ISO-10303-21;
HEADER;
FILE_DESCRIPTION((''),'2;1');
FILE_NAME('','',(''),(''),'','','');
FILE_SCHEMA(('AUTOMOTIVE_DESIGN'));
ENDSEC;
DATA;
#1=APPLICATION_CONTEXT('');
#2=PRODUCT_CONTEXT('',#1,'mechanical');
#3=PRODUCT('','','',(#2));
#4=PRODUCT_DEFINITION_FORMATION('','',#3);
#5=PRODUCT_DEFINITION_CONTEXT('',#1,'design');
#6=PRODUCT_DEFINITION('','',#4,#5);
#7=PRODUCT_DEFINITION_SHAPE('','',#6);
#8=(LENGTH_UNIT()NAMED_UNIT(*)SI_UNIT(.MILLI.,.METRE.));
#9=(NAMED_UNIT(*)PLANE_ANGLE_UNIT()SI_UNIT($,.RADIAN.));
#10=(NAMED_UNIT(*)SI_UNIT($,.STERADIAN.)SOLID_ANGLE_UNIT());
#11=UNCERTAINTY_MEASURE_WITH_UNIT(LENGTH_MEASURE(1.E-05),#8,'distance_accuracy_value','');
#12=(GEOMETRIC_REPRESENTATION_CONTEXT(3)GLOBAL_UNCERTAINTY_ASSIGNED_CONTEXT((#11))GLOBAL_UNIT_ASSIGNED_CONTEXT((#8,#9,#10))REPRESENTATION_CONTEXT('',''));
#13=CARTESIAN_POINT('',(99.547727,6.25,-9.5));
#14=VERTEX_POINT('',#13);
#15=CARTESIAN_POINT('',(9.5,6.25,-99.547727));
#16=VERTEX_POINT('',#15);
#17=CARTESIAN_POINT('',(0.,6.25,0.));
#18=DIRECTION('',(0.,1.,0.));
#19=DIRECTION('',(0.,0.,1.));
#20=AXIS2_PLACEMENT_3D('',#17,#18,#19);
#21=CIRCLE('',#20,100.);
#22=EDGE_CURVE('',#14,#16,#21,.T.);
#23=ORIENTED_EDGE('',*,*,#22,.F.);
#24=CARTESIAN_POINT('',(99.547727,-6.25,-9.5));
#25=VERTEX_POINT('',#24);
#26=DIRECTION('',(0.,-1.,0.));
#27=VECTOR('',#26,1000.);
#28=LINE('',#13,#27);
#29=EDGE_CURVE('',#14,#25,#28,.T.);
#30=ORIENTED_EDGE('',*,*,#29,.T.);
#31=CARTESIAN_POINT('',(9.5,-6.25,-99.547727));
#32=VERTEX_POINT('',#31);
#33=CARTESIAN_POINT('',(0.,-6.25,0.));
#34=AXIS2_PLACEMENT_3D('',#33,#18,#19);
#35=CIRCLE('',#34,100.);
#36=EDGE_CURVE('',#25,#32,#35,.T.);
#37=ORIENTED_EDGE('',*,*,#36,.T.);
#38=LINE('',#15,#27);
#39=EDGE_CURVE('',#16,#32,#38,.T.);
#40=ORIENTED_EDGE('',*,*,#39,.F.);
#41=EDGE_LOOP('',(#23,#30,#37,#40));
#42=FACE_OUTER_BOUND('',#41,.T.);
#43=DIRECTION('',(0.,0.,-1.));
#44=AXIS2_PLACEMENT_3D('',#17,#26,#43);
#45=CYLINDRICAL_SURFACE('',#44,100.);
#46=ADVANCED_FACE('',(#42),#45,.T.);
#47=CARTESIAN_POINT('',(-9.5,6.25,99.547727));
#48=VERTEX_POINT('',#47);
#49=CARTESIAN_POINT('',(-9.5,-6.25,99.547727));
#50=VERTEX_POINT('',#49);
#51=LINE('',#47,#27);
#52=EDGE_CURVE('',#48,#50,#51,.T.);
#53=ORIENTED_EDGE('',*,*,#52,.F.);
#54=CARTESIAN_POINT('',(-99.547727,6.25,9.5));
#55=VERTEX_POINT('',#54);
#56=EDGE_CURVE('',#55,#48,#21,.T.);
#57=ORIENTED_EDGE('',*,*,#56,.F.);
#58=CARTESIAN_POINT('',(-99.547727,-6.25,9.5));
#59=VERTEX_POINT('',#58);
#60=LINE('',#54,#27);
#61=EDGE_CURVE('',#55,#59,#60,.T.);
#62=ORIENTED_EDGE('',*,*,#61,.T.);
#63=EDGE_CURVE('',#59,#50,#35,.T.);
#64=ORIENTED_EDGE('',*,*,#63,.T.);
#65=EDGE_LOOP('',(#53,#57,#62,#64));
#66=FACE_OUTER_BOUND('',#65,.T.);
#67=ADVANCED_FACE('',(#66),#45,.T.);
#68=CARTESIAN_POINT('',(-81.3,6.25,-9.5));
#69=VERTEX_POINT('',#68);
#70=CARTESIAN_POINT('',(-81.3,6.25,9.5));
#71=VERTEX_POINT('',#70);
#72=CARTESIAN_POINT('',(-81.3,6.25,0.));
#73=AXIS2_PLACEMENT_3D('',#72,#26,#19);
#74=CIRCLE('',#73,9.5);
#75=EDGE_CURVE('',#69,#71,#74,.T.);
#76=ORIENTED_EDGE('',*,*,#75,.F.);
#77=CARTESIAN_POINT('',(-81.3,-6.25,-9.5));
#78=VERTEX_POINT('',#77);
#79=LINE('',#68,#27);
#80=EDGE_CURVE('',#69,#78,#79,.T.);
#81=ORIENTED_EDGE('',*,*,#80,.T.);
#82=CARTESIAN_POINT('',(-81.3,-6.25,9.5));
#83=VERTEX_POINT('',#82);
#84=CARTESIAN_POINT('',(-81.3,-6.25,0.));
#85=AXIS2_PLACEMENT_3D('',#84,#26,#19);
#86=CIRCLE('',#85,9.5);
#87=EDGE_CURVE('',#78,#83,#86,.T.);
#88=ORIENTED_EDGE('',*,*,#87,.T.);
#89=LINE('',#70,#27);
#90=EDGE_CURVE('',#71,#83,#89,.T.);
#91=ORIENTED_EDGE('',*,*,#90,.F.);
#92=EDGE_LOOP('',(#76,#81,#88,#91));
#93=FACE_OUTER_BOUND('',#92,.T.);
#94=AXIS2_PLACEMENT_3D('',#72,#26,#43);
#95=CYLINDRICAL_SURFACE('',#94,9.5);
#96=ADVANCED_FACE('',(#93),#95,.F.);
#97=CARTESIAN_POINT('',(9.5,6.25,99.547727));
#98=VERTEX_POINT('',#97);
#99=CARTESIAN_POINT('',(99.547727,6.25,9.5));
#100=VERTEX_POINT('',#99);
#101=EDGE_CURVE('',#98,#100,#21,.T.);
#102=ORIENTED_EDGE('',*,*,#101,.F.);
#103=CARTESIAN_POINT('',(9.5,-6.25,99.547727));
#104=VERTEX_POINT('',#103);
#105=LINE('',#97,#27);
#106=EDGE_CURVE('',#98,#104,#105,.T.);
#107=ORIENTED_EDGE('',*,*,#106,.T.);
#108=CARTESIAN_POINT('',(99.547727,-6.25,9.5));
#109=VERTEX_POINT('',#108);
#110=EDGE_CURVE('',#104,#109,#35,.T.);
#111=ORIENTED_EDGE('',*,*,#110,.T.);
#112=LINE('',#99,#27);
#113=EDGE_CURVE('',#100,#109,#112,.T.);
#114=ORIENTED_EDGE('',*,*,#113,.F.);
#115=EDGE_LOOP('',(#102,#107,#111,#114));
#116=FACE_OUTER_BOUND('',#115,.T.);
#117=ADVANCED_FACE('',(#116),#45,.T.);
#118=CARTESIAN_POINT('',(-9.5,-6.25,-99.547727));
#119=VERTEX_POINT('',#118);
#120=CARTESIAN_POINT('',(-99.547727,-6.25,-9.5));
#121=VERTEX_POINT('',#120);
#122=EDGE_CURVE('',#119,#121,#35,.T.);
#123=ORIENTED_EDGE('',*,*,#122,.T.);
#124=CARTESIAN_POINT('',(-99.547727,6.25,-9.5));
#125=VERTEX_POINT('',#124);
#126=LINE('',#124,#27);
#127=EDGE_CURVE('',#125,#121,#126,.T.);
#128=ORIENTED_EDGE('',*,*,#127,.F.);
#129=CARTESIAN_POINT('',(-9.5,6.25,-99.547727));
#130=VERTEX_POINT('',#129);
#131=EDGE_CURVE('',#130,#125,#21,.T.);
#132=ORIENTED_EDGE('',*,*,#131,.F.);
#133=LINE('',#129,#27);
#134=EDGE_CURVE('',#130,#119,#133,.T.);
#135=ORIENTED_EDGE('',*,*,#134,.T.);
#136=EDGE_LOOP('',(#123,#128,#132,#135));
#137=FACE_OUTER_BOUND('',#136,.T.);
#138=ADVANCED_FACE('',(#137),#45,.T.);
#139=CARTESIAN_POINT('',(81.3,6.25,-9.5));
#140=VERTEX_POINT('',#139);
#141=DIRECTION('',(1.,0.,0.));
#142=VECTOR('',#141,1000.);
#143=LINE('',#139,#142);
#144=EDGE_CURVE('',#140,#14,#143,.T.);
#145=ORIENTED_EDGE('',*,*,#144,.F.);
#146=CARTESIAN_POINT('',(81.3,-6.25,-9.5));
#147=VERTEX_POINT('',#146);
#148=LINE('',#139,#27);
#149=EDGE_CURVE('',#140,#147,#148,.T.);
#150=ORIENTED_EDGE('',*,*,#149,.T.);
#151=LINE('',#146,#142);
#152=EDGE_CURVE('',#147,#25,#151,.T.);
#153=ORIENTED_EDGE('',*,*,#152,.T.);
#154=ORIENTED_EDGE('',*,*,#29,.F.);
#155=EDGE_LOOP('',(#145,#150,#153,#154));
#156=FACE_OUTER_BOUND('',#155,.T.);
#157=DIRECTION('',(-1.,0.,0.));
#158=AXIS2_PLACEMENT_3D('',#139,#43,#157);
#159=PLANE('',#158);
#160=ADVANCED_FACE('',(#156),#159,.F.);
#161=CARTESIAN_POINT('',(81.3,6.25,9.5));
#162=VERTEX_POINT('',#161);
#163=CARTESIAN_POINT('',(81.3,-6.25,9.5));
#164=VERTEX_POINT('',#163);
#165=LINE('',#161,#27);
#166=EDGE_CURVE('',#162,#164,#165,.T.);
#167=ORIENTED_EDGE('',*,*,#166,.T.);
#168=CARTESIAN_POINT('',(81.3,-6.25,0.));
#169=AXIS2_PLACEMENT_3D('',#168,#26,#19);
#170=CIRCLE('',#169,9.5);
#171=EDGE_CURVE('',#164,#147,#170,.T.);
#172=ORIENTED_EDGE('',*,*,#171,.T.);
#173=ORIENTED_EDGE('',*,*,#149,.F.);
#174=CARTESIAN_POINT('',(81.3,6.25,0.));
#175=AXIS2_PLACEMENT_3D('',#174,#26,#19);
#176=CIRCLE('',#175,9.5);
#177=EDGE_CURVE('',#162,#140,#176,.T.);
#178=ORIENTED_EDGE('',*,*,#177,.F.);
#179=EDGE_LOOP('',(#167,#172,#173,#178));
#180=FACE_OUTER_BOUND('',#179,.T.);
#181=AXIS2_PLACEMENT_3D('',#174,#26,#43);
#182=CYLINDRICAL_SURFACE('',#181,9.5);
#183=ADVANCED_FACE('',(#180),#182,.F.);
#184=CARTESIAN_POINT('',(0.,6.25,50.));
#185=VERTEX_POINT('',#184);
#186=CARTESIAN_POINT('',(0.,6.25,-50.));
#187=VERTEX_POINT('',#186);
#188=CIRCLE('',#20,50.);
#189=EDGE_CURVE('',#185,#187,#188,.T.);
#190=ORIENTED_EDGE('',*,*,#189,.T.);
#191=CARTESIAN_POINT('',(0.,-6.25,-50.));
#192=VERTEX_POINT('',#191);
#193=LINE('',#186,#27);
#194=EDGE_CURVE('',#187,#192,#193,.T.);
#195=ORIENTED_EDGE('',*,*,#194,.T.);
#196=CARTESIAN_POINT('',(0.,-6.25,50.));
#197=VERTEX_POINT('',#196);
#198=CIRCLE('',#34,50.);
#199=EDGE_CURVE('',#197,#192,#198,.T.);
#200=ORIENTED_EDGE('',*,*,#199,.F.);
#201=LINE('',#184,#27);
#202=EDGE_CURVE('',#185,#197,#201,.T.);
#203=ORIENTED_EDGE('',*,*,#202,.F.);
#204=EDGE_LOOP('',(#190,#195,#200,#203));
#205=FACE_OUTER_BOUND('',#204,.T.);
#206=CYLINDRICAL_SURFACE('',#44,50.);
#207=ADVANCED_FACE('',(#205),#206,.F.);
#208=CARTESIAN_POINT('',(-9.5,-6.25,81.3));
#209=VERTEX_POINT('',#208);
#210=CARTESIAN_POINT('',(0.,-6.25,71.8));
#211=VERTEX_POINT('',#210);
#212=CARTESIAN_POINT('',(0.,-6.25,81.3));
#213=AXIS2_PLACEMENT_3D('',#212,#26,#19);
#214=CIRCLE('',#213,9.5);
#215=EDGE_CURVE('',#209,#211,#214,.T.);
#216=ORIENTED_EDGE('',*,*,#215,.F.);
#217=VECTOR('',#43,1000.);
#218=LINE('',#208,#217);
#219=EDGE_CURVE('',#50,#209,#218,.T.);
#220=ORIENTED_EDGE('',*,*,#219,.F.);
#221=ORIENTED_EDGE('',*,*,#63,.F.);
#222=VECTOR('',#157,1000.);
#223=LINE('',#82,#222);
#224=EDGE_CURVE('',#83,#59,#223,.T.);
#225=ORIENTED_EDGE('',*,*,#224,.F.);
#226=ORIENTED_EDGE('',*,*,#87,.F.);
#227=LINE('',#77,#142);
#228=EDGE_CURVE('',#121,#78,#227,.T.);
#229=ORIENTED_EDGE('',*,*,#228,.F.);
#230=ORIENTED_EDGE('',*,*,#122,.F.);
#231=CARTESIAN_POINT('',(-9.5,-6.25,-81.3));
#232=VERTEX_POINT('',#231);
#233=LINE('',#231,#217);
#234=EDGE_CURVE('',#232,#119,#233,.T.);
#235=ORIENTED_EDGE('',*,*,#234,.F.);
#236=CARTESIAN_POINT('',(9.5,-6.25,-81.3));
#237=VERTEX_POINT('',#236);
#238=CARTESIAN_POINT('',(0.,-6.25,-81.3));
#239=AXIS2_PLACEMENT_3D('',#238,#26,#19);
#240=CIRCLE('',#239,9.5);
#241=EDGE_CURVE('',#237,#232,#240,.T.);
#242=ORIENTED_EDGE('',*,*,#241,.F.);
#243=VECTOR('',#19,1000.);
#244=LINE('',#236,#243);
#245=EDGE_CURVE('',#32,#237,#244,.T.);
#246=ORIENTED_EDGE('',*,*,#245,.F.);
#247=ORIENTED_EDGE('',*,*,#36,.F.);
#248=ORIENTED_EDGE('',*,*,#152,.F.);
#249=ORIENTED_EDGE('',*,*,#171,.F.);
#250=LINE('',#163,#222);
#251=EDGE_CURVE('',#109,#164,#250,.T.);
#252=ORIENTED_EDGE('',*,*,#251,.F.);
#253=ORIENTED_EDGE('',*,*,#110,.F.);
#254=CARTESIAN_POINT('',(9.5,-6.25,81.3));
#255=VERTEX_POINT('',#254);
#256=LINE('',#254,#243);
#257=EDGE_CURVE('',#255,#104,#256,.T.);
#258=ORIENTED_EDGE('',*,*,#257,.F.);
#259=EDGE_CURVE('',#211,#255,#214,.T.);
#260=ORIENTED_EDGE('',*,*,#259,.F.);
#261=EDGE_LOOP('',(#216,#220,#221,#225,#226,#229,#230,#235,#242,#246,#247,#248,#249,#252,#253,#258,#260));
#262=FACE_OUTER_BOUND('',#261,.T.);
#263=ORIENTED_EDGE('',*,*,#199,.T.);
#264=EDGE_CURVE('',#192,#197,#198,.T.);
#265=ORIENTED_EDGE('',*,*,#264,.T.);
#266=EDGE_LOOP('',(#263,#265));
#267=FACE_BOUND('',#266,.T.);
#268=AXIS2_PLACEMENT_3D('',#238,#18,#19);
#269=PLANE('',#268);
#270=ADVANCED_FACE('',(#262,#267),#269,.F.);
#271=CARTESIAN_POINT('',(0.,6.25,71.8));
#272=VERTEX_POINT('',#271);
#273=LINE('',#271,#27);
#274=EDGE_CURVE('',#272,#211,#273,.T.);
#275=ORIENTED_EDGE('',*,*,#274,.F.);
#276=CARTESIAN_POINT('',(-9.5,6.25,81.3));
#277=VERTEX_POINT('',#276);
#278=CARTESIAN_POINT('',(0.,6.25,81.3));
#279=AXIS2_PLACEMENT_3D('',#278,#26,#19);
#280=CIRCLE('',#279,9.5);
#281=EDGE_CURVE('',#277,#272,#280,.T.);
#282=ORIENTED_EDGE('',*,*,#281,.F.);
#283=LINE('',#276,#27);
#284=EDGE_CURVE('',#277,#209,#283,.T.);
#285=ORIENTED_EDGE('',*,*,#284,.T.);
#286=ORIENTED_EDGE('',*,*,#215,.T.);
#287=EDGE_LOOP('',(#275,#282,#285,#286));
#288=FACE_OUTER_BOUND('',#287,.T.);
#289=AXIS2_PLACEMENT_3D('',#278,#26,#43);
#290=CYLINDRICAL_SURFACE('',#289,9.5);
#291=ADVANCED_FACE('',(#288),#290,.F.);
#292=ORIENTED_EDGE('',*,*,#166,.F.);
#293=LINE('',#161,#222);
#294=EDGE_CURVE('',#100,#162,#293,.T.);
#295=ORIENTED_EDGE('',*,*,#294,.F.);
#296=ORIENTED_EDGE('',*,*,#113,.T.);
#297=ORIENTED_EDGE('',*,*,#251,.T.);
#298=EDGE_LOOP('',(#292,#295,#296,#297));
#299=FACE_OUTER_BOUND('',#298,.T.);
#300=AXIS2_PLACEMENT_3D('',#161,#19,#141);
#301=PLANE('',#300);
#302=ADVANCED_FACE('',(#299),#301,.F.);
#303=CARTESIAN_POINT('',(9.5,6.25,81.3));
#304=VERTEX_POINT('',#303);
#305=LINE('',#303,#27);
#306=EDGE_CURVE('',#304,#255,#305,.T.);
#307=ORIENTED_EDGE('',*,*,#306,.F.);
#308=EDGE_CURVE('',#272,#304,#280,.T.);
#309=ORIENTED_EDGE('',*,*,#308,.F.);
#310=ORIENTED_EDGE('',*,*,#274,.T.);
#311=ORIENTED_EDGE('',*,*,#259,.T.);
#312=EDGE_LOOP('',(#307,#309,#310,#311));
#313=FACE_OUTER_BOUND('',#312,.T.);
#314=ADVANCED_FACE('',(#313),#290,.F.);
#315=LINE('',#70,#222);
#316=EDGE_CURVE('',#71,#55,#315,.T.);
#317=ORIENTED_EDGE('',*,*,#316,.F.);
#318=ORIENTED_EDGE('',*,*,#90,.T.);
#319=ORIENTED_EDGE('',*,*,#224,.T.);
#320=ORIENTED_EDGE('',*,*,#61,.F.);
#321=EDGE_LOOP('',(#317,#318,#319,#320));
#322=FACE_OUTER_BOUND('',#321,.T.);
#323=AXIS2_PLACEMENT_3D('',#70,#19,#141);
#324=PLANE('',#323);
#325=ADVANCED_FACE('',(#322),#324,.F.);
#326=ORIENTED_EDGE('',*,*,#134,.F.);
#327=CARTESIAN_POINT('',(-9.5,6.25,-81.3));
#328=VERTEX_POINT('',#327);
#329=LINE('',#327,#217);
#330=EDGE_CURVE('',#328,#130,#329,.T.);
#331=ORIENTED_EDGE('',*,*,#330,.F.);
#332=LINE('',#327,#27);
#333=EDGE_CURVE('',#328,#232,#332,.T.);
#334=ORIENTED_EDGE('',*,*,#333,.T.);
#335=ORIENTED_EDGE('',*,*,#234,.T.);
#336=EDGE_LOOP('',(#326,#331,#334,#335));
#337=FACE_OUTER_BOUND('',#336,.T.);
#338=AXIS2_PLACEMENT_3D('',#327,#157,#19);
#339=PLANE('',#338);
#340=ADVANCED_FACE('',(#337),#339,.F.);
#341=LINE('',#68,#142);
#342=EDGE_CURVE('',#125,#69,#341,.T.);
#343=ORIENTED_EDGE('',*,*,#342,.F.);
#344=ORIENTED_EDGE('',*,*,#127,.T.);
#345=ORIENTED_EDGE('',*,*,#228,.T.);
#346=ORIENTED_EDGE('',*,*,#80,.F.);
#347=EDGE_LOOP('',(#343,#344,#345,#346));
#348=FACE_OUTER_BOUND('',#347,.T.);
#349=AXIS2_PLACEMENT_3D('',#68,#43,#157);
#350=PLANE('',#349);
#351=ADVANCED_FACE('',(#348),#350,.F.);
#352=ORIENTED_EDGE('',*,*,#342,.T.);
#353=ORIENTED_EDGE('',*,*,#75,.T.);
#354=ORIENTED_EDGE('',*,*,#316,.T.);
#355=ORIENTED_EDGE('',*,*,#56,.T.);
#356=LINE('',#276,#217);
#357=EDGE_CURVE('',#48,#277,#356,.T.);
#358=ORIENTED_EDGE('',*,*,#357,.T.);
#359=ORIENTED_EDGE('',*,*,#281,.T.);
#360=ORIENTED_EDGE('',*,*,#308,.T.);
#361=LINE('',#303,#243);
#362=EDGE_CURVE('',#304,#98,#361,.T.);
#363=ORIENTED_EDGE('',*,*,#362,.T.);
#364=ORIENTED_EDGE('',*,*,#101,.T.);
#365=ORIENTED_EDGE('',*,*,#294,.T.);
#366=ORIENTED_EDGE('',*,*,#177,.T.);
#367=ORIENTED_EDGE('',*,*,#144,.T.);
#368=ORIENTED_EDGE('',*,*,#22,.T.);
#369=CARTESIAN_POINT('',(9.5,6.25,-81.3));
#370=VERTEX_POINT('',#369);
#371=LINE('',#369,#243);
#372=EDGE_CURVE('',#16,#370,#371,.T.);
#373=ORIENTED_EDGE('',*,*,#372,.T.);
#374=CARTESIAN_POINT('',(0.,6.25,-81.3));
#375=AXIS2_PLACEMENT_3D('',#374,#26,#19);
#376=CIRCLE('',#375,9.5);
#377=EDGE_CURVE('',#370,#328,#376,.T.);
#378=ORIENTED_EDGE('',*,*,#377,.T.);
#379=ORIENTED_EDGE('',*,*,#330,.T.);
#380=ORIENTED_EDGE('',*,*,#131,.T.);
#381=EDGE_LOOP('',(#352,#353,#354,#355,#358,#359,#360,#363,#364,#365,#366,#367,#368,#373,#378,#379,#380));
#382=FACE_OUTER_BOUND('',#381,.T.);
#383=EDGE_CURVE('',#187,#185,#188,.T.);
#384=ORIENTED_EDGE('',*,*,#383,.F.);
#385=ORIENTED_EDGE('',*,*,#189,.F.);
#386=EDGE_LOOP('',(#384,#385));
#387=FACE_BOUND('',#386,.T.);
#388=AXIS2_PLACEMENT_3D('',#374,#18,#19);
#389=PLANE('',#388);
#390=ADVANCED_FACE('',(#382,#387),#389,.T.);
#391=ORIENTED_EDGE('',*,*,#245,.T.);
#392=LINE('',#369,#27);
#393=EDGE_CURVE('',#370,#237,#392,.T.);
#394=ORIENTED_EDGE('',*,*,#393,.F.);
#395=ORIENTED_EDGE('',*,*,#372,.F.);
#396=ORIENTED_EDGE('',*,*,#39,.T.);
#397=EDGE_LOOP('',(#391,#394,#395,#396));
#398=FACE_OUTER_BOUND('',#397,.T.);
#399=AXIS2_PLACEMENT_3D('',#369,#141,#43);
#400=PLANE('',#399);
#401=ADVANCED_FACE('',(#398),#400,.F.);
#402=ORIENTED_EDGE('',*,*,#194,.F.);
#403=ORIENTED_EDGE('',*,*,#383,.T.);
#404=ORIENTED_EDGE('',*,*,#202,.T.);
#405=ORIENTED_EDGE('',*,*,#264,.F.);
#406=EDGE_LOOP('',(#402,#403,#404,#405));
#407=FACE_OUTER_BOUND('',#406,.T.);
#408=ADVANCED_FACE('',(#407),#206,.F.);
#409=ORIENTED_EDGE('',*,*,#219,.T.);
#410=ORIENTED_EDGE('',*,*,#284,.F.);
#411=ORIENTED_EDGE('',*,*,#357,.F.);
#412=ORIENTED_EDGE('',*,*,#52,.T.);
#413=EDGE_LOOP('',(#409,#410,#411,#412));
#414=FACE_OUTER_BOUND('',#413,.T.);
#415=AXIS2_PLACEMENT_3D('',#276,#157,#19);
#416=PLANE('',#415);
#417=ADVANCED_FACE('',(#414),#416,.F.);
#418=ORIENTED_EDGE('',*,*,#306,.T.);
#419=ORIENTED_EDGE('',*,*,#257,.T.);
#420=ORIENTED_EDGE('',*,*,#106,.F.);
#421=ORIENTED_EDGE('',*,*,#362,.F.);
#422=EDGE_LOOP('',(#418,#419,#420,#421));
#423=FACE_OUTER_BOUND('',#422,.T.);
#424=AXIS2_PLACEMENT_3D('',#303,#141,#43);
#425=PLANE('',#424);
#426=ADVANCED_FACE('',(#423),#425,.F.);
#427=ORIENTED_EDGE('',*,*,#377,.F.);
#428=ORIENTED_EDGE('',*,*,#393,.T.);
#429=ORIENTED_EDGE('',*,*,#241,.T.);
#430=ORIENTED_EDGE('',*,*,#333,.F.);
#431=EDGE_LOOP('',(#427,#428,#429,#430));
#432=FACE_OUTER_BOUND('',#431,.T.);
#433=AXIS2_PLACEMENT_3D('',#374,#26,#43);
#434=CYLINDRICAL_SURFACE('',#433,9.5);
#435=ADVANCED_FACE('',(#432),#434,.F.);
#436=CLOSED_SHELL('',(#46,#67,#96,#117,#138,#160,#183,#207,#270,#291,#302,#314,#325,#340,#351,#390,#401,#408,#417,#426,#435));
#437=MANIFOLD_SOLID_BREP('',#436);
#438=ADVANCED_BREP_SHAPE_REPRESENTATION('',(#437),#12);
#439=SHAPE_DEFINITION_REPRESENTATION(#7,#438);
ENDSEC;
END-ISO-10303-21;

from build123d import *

# Parameters (mm, degrees)
DISK_PROFILE_SKETCH_R       = 50
SLOTTED_DISK_200X12_5_DEPTH = 6.25


with BuildPart() as part:
    # Disk Profile Sketch → Slotted Disk Ø200x12.5 (new, symmetric)
    with BuildSketch(Plane(origin=(0, 0, 0), x_dir=(1, 0, 0), z_dir=(0, 1, 0))):
        with BuildLine():
            Line((-9.5, 81.3), (-9.5, 99.547727247))
            ThreePointArc((-9.5, 99.547727247), (-70.710678119, 70.710678119), (-99.547727247, 9.5))
            Line((-99.547727247, 9.5), (-81.3, 9.5))
            ThreePointArc((-81.3, 9.5), (-71.8, 0), (-81.3, -9.5))
            Line((-81.3, -9.5), (-99.547727247, -9.5))
            ThreePointArc((-99.547727247, -9.5), (-70.710678119, -70.710678119), (-9.5, -99.547727247))
            Line((-9.5, -99.547727247), (-9.5, -81.3))
            ThreePointArc((-9.5, -81.3), (0, -71.8), (9.5, -81.3))
            Line((9.5, -81.3), (9.5, -99.547727247))
            ThreePointArc((9.5, -99.547727247), (70.710678119, -70.710678119), (99.547727247, -9.5))
            Line((99.547727247, -9.5), (81.3, -9.5))
            ThreePointArc((81.3, -9.5), (71.8, 0), (81.3, 9.5))
            Line((81.3, 9.5), (99.547727247, 9.5))
            ThreePointArc((99.547727247, 9.5), (70.710678119, 70.710678119), (9.5, 99.547727247))
            Line((9.5, 99.547727247), (9.5, 81.3))
            ThreePointArc((9.5, 81.3), (0, 71.8), (-9.5, 81.3))
        make_face()
        with Locations(Location((0, 0, 0), (0, 0, 270))):
            Circle(DISK_PROFILE_SKETCH_R, mode=Mode.SUBTRACT)
    extrude(amount=SLOTTED_DISK_200X12_5_DEPTH, both=True)


solid = part.part
